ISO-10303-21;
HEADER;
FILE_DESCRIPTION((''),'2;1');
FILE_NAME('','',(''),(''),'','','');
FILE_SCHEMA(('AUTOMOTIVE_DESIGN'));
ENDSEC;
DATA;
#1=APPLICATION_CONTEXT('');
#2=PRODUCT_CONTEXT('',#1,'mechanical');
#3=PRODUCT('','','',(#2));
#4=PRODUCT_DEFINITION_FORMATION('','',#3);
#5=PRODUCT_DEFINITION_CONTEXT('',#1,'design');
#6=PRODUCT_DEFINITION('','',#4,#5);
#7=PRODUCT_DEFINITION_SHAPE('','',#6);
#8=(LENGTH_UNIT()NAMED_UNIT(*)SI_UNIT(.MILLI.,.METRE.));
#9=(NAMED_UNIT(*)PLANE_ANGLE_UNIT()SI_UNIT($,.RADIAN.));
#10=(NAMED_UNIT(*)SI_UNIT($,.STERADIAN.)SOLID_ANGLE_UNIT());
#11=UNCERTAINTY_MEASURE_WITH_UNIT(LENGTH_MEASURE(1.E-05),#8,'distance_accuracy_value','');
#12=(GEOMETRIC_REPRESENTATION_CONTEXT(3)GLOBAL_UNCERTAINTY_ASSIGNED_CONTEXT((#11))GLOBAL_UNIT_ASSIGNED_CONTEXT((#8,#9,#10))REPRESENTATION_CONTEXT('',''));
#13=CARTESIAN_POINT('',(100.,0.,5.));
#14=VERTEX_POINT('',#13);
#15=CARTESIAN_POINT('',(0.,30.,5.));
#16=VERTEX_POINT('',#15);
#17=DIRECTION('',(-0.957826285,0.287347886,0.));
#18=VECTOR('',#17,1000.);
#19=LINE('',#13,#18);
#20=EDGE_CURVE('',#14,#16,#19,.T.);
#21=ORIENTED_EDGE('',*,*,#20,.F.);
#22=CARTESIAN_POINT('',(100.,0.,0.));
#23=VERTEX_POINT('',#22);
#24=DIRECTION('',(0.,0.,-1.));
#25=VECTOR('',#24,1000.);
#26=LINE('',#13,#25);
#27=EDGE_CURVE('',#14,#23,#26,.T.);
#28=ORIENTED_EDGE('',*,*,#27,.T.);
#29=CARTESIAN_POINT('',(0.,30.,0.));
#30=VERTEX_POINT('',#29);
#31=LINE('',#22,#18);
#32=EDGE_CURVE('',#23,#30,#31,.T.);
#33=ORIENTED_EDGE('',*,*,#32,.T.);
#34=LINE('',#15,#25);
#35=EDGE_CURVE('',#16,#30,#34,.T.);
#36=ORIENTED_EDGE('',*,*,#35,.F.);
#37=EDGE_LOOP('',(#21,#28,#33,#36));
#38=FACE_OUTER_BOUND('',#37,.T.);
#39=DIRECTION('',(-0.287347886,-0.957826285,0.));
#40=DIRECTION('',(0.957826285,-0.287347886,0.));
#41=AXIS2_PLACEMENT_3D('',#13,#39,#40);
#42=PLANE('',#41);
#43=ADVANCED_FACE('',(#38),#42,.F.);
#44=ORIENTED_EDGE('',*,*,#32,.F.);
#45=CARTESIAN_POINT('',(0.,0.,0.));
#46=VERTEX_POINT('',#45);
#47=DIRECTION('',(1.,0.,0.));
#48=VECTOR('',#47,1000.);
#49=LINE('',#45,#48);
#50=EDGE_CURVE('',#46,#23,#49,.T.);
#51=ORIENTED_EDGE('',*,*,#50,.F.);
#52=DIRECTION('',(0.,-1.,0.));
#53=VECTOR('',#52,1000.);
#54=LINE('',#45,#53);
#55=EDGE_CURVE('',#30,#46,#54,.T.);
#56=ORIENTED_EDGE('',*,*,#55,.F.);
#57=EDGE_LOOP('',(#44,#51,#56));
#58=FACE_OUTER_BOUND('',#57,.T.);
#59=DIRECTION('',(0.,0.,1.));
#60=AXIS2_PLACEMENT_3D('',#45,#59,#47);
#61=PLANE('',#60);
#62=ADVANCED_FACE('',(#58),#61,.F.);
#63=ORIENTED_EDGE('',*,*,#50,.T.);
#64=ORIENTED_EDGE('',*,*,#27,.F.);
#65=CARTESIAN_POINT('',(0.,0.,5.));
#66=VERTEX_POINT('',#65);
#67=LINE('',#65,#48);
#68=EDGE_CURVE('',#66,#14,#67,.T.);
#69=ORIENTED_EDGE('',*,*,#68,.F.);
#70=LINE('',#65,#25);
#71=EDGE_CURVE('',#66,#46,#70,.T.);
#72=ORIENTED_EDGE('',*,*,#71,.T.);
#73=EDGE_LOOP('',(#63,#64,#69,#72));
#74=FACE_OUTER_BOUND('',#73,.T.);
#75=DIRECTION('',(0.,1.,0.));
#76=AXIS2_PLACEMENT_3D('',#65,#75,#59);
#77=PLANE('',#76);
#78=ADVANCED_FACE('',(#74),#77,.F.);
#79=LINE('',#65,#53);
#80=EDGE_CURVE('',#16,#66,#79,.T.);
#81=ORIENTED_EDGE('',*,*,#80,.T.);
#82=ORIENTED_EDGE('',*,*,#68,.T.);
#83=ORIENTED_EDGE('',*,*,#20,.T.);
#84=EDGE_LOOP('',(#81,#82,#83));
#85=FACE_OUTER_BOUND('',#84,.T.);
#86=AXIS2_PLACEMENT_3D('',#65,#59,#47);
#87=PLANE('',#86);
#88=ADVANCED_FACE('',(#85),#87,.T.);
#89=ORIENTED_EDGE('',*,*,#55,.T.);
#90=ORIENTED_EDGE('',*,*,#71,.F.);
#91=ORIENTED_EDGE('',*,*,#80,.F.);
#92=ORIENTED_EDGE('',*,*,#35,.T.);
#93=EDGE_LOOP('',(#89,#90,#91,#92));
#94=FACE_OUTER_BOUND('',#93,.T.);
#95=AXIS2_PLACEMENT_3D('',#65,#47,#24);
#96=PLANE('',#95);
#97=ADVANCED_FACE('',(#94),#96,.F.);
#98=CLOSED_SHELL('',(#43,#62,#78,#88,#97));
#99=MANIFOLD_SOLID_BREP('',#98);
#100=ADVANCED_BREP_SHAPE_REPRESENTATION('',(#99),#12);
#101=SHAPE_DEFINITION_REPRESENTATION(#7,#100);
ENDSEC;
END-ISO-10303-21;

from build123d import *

# Parameters (mm, degrees)
EXTRUDE_1_DEPTH = 5


with BuildPart() as part:
    # 草图1 → 凸台-拉伸1 (new body)
    with BuildSketch(Plane.XY):
        Polygon((0, 0), (0, 30), (100, 0), align=None)
    extrude(amount=EXTRUDE_1_DEPTH)


solid = part.part
